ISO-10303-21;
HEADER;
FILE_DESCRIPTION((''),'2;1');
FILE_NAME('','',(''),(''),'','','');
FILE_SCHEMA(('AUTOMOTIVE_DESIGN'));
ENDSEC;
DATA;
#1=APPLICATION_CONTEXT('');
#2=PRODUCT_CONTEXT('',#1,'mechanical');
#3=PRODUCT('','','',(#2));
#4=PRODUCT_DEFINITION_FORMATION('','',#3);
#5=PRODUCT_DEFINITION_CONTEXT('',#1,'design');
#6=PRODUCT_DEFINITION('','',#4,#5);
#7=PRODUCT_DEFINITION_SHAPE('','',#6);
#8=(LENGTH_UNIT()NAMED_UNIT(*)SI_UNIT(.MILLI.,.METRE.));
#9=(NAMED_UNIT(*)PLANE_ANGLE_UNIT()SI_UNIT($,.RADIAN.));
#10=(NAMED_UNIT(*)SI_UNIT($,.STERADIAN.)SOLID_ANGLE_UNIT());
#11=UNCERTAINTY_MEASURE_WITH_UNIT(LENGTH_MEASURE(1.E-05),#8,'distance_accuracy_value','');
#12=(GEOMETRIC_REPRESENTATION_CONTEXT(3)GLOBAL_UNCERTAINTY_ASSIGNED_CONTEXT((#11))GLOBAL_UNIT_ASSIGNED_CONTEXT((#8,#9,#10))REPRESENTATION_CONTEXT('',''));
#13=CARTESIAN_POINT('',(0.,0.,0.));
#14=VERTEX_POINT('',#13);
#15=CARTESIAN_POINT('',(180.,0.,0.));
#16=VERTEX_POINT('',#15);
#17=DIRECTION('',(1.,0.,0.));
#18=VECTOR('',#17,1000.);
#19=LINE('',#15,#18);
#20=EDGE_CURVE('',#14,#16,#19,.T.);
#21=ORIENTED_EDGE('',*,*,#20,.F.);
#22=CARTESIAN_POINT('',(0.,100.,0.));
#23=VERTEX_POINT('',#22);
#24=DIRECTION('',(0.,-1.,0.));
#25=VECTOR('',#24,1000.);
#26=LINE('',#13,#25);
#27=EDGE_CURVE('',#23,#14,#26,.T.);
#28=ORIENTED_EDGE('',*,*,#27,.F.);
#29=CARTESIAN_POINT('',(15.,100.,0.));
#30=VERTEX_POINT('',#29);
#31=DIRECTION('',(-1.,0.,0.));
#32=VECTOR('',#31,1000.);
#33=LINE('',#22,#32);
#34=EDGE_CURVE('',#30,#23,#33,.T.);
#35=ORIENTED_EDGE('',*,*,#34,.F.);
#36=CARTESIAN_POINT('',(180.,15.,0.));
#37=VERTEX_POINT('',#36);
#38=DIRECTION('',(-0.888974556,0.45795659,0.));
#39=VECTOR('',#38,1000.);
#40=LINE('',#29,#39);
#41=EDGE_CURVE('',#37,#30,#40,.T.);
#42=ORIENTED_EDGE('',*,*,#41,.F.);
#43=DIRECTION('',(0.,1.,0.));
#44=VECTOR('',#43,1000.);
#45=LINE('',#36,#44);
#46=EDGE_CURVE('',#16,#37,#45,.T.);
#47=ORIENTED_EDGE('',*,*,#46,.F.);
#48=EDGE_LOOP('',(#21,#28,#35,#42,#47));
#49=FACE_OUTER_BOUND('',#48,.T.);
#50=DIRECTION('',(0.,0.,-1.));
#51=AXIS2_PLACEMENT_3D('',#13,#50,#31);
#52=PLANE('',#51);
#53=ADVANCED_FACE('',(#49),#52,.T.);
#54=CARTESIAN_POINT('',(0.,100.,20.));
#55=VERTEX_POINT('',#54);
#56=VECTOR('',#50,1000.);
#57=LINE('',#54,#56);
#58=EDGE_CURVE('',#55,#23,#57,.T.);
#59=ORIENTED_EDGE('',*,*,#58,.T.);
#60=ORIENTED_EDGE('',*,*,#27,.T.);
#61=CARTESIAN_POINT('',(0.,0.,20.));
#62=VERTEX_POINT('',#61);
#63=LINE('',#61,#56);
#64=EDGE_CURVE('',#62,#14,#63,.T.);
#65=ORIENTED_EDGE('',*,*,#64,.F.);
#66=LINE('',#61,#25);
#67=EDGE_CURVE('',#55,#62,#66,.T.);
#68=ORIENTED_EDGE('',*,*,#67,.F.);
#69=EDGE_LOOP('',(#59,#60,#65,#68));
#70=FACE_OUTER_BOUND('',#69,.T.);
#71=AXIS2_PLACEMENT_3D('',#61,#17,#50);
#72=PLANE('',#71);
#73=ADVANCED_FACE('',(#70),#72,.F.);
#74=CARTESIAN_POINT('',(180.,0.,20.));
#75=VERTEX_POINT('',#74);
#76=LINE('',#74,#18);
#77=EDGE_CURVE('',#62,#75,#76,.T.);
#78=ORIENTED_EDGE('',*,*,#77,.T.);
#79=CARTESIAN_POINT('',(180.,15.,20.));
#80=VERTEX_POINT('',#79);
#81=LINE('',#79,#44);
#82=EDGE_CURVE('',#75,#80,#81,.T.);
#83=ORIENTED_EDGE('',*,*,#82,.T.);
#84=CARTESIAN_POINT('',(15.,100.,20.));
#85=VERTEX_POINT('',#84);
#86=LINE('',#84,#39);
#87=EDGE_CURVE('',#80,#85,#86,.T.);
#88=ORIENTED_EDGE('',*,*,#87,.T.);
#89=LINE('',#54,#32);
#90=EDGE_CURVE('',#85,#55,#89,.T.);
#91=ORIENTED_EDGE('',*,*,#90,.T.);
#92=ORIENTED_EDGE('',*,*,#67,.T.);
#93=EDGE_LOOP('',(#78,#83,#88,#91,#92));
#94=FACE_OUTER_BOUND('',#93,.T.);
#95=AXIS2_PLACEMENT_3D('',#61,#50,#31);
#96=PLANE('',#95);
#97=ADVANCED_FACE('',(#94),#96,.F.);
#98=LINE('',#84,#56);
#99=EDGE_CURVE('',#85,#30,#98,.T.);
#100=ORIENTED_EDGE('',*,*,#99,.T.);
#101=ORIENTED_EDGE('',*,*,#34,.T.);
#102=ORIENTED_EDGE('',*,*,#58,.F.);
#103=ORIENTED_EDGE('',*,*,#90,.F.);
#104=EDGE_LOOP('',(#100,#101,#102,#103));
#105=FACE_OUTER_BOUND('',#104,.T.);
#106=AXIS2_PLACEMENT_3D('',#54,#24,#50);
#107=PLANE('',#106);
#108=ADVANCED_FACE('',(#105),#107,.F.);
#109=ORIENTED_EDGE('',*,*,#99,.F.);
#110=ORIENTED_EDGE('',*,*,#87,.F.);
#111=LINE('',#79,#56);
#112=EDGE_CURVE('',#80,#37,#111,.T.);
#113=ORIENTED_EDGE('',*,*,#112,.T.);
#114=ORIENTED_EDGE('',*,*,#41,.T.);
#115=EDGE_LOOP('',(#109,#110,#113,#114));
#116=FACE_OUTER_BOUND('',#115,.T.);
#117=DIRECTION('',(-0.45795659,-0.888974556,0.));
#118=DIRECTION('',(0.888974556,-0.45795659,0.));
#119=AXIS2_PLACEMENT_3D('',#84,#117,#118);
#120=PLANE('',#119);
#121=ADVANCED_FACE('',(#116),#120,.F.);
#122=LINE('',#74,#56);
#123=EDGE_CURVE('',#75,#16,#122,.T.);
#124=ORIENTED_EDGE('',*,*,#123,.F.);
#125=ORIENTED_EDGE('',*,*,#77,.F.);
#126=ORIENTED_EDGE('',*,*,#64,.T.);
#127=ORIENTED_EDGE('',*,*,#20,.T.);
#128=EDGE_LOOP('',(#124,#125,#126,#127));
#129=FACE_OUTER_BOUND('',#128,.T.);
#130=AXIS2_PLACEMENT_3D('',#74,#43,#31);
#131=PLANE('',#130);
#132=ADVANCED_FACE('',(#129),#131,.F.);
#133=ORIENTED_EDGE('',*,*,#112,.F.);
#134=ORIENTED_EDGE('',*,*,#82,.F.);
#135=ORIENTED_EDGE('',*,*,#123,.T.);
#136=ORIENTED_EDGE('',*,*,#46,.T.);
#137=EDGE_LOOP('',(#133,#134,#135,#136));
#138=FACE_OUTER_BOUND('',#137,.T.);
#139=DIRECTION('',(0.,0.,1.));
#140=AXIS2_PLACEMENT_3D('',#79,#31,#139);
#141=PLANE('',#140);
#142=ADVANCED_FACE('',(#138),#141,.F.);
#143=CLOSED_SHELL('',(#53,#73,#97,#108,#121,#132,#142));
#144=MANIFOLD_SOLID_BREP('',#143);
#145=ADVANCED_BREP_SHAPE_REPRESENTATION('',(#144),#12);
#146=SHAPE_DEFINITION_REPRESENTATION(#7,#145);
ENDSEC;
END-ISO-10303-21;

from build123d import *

# Parameters (mm, degrees)
BOSS_EXTRUDE1_DEPTH = 20


with BuildPart() as part:
    # Sketch1 → Boss-Extrude1 (new body)
    with BuildSketch(Plane.XY):
        Polygon((0, 0), (0, 100), (15, 100), (180, 15), (180, 0), align=None)
    extrude(amount=BOSS_EXTRUDE1_DEPTH)


solid = part.part
